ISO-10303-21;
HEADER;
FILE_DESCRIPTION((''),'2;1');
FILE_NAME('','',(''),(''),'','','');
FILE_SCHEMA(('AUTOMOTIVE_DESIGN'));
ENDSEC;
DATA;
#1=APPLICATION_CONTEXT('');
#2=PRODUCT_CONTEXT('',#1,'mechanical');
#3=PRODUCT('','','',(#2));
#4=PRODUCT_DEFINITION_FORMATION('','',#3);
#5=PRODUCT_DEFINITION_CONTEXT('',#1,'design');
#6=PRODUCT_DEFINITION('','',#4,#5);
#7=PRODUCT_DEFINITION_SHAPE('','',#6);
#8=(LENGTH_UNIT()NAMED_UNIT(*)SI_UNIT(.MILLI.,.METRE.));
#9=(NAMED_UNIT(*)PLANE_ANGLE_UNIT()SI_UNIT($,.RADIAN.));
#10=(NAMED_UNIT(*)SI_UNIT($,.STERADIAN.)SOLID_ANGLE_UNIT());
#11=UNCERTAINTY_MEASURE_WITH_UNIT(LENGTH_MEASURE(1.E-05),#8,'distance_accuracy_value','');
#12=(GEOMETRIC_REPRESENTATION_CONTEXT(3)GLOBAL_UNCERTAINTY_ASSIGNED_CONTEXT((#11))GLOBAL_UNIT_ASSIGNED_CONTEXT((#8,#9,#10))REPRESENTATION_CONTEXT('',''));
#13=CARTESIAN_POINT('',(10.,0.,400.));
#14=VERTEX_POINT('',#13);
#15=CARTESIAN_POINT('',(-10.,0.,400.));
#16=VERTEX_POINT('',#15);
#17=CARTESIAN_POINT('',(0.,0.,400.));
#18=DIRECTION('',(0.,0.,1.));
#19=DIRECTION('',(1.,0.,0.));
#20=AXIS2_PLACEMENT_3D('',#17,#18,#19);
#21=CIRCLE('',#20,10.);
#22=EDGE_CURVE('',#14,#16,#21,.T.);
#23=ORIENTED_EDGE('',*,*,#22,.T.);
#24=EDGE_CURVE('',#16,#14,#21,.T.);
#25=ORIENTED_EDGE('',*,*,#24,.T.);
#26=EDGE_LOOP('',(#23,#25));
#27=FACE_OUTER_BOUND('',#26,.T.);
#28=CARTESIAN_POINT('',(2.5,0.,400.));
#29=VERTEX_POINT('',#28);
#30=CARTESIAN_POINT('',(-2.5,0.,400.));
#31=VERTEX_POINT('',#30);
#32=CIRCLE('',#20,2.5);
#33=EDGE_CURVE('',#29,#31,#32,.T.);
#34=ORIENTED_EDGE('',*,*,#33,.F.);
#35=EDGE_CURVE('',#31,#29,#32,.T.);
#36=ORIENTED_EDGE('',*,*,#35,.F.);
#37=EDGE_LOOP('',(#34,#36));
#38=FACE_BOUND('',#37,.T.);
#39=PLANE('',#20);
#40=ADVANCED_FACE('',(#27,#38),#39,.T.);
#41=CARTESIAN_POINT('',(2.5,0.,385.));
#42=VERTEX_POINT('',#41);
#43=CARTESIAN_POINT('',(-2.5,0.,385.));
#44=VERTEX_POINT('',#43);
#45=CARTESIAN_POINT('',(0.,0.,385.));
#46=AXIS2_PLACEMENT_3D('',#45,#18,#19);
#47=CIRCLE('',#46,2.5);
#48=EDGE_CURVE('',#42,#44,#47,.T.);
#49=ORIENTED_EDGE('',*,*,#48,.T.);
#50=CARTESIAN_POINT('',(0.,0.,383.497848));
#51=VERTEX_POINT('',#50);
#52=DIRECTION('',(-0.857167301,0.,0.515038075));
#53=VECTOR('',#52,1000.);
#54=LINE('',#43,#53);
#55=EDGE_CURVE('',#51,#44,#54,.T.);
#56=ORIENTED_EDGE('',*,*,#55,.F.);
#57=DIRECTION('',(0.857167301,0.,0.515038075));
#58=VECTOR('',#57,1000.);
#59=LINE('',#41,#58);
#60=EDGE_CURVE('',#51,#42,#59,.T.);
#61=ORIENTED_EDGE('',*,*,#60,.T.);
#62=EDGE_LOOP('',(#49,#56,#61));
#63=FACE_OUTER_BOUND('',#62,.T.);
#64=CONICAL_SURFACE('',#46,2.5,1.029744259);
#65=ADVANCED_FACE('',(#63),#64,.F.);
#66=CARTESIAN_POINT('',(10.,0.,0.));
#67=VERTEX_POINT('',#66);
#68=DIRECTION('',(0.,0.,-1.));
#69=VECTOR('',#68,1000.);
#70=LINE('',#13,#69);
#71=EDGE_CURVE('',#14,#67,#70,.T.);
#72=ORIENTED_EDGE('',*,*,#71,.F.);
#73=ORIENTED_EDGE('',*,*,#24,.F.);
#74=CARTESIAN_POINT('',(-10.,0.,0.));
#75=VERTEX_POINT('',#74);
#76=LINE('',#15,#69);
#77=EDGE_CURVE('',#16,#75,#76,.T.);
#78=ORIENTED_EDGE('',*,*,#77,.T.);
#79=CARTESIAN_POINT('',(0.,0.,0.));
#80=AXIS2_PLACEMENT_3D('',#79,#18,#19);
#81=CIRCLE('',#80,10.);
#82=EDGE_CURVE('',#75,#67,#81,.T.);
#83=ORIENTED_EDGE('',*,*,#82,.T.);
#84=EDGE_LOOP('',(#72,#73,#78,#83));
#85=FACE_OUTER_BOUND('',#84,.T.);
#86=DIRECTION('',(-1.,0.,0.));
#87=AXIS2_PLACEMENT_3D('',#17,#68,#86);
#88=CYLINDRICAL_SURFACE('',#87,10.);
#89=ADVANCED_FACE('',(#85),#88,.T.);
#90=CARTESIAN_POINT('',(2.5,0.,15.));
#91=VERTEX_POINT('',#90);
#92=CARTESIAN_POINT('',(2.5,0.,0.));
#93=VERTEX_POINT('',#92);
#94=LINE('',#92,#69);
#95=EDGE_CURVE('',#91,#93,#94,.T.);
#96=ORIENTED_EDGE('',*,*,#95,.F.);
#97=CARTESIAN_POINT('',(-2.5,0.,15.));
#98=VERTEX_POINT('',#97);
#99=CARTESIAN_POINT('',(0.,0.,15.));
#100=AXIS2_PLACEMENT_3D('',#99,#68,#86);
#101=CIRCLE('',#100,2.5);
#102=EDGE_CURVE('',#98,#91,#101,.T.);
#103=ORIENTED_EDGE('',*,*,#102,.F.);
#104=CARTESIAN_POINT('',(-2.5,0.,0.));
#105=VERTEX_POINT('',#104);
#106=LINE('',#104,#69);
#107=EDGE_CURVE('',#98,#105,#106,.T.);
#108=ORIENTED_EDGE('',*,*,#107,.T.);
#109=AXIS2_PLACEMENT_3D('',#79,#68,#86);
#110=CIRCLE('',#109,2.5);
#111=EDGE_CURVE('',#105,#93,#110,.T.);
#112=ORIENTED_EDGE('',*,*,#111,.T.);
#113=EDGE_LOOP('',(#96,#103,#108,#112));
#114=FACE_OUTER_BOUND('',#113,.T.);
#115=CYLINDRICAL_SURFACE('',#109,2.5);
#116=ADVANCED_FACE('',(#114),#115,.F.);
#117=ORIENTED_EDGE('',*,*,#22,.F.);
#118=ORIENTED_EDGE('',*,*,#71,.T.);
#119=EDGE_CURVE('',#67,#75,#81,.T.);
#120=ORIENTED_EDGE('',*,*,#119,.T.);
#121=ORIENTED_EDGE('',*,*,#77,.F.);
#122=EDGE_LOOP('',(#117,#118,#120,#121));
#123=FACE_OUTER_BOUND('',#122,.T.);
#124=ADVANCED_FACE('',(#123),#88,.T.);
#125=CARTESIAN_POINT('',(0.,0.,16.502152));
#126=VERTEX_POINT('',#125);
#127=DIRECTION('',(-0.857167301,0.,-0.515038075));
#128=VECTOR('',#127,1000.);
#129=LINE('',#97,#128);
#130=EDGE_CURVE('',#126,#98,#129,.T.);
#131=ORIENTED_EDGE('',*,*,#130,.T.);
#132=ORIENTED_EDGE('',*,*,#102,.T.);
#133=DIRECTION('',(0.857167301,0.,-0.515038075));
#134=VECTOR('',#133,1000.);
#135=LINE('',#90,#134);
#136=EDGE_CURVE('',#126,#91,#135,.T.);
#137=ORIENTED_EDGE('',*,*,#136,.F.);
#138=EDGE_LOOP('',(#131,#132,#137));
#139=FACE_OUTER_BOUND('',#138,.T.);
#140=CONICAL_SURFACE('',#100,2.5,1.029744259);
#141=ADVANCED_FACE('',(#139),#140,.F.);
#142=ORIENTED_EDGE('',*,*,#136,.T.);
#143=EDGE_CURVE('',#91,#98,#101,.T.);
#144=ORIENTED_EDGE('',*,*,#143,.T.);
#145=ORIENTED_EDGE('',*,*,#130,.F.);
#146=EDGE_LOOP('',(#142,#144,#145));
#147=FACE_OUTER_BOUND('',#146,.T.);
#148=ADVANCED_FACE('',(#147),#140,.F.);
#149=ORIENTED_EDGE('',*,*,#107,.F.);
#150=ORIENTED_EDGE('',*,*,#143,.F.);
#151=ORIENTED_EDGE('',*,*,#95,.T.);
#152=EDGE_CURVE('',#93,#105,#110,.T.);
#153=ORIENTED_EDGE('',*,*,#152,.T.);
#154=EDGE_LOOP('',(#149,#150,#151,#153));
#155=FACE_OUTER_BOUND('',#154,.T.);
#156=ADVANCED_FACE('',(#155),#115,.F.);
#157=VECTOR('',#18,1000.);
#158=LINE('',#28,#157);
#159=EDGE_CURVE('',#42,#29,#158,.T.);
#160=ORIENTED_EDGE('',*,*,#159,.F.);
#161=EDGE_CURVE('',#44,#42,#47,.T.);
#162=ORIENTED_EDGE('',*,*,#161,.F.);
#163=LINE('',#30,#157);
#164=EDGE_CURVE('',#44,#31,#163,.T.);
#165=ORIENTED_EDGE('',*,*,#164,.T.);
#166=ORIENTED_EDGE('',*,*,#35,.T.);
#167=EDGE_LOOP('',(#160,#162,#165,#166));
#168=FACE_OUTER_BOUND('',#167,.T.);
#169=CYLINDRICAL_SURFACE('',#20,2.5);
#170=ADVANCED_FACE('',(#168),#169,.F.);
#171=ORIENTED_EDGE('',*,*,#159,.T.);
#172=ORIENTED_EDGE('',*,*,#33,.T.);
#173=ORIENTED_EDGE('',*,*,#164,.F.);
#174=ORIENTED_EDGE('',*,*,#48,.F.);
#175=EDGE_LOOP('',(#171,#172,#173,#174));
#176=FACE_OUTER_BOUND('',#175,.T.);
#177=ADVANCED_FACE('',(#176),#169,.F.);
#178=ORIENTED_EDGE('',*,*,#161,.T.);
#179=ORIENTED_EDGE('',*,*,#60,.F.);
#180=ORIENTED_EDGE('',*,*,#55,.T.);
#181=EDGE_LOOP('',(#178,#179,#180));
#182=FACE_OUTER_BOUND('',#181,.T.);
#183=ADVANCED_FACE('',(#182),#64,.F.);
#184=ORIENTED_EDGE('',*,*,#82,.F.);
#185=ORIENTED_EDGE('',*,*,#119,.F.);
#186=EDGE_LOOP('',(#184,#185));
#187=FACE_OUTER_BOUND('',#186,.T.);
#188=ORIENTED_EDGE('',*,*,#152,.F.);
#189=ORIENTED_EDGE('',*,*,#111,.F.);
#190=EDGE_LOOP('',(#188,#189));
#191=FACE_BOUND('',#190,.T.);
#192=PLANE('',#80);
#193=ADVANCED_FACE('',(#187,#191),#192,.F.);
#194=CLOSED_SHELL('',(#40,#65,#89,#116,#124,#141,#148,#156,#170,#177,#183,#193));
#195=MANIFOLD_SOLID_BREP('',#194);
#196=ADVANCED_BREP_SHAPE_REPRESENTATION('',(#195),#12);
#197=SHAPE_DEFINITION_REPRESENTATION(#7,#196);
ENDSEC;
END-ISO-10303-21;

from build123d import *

# Parameters (mm, degrees)
SKETCH1_R             = 10
BOSS_EXTRUDE1_DEPTH   = 400
M6_TAPPED_HOLE1_D     = 5
M6_TAPPED_HOLE1_DEPTH = 15
M6_TAPPED_HOLE1_TIP   = 1.502151548
M6_TAPPED_HOLE2_D     = 5
M6_TAPPED_HOLE2_DEPTH = 15
M6_TAPPED_HOLE2_TIP   = 1.502151548


with BuildPart() as part:
    # Sketch1 → Boss-Extrude1 (new body)
    with BuildSketch(Plane.XY):
        Circle(SKETCH1_R)
    extrude(amount=BOSS_EXTRUDE1_DEPTH)

    # M6 Tapped Hole1
    with Locations(Plane.XY.offset(400)):
        with Locations((0, 0)):
            Hole(M6_TAPPED_HOLE1_D / 2, depth=M6_TAPPED_HOLE1_DEPTH)
            with Locations((0, 0, -(M6_TAPPED_HOLE1_DEPTH + M6_TAPPED_HOLE1_TIP / 2))):  # 118° drill point
                Cone(0, M6_TAPPED_HOLE1_D / 2, M6_TAPPED_HOLE1_TIP, mode=Mode.SUBTRACT)

    # M6 Tapped Hole2
    with Locations(Plane(origin=(0, 0, 0), x_dir=(-1, 0, 0), z_dir=(0, 0, -1))):
        with Locations((0, 0)):
            Hole(M6_TAPPED_HOLE2_D / 2, depth=M6_TAPPED_HOLE2_DEPTH)
            with Locations((0, 0, -(M6_TAPPED_HOLE2_DEPTH + M6_TAPPED_HOLE2_TIP / 2))):  # 118° drill point
                Cone(0, M6_TAPPED_HOLE2_D / 2, M6_TAPPED_HOLE2_TIP, mode=Mode.SUBTRACT)


solid = part.part
